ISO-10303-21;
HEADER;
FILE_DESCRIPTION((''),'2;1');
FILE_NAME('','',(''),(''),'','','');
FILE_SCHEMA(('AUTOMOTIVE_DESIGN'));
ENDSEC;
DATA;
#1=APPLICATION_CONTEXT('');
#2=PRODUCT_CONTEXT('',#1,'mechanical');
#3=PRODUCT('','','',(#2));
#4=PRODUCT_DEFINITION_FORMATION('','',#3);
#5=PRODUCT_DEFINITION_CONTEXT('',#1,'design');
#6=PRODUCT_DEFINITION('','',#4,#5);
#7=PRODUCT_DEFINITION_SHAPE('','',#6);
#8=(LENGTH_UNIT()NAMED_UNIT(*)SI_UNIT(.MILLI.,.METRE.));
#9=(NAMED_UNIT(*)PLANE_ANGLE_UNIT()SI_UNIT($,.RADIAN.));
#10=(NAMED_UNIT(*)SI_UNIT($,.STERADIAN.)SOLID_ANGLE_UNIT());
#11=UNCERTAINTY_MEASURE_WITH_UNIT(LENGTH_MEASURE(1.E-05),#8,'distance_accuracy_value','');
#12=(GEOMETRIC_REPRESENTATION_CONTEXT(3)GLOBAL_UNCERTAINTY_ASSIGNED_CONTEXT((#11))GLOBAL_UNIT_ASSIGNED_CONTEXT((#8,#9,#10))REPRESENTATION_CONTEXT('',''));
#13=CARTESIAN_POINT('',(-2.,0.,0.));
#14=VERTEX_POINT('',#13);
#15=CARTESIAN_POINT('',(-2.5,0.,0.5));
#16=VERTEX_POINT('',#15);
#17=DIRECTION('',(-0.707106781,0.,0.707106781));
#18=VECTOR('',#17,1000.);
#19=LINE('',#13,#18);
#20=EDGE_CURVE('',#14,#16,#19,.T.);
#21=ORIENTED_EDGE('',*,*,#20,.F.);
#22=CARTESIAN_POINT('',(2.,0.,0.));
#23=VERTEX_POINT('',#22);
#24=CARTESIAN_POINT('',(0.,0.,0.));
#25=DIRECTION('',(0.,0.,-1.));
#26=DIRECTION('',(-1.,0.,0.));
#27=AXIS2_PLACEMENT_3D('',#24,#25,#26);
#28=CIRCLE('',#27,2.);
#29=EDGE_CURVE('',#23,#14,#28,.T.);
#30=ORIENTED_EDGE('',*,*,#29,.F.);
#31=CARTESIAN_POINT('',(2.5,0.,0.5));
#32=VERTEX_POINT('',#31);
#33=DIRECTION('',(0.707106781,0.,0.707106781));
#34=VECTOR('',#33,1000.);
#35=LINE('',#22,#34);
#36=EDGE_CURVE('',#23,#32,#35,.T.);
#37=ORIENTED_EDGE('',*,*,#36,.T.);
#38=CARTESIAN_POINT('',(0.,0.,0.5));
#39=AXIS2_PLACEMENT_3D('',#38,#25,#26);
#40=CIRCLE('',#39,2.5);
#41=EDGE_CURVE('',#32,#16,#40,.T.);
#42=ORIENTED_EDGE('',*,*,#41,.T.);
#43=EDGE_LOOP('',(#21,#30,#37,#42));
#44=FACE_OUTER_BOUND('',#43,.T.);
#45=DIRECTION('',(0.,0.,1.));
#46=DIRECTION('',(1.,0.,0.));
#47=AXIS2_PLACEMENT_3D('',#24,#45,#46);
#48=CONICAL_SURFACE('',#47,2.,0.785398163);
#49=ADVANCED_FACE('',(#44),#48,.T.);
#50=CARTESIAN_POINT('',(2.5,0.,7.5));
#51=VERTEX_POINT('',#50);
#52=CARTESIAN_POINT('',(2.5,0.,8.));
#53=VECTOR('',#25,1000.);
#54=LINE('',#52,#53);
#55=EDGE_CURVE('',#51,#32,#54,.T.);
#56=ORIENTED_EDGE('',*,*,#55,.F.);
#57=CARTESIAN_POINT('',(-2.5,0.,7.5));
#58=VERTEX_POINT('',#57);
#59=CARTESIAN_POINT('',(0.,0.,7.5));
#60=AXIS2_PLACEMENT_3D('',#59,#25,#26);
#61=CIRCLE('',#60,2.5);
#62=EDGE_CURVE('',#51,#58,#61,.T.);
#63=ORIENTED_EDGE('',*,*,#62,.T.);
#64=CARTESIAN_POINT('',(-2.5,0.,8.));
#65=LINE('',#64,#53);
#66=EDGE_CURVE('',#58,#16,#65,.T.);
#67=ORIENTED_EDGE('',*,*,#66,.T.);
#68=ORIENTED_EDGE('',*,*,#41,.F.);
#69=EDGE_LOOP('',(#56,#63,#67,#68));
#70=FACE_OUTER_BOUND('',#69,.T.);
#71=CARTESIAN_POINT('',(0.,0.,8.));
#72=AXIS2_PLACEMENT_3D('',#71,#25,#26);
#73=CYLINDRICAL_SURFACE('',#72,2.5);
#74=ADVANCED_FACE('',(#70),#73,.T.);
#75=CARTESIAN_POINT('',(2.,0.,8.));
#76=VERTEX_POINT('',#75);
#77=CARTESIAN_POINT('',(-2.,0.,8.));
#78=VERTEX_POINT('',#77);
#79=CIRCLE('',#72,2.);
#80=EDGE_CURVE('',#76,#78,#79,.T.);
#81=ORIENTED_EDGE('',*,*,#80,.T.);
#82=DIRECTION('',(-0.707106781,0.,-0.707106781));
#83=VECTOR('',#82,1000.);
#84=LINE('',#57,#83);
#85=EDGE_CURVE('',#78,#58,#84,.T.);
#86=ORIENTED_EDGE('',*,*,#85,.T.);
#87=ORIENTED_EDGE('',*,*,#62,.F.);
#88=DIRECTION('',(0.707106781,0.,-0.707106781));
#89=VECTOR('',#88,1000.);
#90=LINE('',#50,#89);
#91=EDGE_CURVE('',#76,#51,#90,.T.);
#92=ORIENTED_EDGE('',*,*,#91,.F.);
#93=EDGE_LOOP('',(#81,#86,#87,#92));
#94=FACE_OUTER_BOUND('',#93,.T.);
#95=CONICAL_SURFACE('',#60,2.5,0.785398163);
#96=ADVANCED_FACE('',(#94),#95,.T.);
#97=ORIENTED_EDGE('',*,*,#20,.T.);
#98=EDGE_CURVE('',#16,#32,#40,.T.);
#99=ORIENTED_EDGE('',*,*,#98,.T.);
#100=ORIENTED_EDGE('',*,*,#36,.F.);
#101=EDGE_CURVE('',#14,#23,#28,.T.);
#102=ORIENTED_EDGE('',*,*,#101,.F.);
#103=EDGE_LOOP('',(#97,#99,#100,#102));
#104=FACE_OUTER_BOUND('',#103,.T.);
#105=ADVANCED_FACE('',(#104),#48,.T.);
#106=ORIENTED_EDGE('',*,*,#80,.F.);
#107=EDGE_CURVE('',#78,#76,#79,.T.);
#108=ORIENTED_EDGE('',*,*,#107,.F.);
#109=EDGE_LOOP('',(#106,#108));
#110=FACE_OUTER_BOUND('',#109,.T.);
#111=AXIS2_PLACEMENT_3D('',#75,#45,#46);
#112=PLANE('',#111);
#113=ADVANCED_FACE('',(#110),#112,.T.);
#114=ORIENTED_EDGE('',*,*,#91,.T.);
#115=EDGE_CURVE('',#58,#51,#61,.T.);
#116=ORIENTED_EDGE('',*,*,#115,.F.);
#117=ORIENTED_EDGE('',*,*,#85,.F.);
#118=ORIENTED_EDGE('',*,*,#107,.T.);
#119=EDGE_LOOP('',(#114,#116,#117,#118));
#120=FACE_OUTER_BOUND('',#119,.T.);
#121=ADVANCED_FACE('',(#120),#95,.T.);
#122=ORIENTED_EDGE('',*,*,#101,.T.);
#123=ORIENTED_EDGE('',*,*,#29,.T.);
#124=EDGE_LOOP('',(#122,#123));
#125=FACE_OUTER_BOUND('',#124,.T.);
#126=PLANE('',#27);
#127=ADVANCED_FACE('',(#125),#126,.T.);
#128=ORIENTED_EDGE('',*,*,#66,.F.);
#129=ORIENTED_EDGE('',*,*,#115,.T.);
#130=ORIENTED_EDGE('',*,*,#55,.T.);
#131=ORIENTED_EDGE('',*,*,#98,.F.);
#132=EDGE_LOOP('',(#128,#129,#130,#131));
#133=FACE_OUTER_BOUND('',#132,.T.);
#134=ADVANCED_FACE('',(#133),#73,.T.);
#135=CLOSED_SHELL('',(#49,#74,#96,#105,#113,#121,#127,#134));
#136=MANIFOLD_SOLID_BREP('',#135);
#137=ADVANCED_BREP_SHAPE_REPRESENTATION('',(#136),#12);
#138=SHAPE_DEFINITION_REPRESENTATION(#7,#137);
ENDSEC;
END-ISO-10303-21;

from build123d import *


with BuildPart() as part:
    # Sketch1 → Revolve1 (revolve)
    with BuildSketch(Plane.XZ, mode=Mode.PRIVATE) as revolve1_sk:
        Polygon((2, 8), (0, 8), (0, 0), (2, 0), (2.5, 0.5), (2.5, 7.5), align=None)
    revolve(revolve1_sk.sketch.rotate(Axis((0, 0, 8), (0, 0, -1)), 180), axis=Axis((0, 0, 8), (0, 0, -1)))


solid = part.part
